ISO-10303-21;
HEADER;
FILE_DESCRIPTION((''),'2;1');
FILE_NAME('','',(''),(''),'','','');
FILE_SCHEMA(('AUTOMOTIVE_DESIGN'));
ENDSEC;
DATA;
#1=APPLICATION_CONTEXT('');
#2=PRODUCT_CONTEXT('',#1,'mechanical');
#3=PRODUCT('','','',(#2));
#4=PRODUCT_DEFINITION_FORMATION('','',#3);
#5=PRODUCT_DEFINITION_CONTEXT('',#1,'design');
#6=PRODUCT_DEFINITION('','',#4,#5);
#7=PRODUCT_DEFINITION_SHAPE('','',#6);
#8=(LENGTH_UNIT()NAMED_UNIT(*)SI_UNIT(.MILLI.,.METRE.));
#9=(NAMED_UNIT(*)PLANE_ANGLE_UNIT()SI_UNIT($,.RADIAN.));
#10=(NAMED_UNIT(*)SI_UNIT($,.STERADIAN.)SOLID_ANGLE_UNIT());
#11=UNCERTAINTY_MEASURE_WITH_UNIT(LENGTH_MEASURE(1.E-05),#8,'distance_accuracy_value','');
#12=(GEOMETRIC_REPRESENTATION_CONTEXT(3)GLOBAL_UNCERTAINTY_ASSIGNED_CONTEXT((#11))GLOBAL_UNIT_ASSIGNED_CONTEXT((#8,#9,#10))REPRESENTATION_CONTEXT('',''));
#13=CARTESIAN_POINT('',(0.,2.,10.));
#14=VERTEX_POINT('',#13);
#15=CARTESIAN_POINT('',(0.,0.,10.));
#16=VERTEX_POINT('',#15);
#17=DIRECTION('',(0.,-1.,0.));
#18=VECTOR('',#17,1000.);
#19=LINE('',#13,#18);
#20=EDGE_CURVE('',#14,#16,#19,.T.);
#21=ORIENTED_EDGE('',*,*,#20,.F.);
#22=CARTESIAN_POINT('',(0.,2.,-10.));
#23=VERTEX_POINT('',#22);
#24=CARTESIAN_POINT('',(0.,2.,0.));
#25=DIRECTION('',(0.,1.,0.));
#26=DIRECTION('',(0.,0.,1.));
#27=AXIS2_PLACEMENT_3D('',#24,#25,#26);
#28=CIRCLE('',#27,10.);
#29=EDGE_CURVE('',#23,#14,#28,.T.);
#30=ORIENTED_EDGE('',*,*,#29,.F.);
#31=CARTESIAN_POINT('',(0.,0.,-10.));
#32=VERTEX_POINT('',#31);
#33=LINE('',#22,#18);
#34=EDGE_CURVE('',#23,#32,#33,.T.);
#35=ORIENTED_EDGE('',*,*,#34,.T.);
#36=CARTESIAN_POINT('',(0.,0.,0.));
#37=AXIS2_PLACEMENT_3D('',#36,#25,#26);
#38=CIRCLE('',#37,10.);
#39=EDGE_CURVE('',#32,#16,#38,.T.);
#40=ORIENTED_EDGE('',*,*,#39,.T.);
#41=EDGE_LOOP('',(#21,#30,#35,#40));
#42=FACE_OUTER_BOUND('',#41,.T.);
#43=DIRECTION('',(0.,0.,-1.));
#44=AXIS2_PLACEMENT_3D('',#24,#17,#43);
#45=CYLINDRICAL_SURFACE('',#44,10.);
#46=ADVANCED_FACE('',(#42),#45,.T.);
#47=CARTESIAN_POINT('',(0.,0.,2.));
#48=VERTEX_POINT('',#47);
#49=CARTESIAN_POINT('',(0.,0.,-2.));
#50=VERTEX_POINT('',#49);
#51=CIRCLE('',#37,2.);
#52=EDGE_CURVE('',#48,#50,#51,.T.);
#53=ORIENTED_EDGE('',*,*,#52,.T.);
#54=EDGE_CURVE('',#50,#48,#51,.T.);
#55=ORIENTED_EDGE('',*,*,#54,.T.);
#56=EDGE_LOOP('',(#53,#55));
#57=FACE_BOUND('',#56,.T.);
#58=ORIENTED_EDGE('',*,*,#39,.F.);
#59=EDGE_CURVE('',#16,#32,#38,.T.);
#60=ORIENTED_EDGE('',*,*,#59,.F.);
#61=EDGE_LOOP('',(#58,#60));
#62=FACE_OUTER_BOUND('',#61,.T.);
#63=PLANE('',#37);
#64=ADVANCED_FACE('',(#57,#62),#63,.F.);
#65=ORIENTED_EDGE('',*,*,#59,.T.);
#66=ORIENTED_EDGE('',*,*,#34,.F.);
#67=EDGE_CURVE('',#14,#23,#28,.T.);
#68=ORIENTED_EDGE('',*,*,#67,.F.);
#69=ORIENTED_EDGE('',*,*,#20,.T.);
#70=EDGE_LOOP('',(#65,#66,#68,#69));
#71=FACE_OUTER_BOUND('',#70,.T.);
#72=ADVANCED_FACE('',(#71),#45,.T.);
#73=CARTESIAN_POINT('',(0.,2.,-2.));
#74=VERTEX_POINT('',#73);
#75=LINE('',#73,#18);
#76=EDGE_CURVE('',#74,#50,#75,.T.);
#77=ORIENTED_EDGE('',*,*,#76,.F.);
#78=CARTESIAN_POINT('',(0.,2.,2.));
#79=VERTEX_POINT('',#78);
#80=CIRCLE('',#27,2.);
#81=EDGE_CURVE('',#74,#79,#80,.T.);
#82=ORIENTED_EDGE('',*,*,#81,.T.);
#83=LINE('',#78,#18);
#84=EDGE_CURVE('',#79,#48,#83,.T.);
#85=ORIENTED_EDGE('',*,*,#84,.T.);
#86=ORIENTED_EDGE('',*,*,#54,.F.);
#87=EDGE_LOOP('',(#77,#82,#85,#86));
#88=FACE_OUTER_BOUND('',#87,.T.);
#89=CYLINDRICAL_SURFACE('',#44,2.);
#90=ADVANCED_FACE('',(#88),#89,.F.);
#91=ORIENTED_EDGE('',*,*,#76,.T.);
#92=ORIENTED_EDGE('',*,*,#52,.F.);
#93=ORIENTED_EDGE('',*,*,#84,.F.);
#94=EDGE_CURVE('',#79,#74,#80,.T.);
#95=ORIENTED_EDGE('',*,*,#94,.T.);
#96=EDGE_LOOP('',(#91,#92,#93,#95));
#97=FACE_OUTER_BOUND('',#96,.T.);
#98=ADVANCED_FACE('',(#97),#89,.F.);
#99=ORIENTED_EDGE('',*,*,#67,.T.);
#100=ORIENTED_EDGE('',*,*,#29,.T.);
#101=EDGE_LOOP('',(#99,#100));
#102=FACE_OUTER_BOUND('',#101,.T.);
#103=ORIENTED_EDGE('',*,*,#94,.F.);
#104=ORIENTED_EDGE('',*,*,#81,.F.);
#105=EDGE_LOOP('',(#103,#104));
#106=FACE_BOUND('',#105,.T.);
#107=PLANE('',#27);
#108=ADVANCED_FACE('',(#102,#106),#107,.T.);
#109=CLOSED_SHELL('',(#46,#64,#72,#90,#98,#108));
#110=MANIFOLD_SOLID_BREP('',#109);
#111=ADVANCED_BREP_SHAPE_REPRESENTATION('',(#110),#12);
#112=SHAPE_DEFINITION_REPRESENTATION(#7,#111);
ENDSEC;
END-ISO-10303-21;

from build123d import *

# Parameters (mm, degrees)
SKETCH1_R           = 10
SKETCH1_R_2         = 2
BOSS_EXTRUDE1_DEPTH = 2


with BuildPart() as part:
    # Sketch1 → Boss-Extrude1 (new body)
    with BuildSketch(Plane(origin=(0, 0, 0), x_dir=(1, 0, 0), z_dir=(0, 1, 0))):
        with Locations(Location((0, 0, 0), (0, 0, 270))):
            Circle(SKETCH1_R)
        with Locations(Location((0, 0, 0), (0, 0, 270))):
            Circle(SKETCH1_R_2, mode=Mode.SUBTRACT)
    extrude(amount=BOSS_EXTRUDE1_DEPTH)


solid = part.part
